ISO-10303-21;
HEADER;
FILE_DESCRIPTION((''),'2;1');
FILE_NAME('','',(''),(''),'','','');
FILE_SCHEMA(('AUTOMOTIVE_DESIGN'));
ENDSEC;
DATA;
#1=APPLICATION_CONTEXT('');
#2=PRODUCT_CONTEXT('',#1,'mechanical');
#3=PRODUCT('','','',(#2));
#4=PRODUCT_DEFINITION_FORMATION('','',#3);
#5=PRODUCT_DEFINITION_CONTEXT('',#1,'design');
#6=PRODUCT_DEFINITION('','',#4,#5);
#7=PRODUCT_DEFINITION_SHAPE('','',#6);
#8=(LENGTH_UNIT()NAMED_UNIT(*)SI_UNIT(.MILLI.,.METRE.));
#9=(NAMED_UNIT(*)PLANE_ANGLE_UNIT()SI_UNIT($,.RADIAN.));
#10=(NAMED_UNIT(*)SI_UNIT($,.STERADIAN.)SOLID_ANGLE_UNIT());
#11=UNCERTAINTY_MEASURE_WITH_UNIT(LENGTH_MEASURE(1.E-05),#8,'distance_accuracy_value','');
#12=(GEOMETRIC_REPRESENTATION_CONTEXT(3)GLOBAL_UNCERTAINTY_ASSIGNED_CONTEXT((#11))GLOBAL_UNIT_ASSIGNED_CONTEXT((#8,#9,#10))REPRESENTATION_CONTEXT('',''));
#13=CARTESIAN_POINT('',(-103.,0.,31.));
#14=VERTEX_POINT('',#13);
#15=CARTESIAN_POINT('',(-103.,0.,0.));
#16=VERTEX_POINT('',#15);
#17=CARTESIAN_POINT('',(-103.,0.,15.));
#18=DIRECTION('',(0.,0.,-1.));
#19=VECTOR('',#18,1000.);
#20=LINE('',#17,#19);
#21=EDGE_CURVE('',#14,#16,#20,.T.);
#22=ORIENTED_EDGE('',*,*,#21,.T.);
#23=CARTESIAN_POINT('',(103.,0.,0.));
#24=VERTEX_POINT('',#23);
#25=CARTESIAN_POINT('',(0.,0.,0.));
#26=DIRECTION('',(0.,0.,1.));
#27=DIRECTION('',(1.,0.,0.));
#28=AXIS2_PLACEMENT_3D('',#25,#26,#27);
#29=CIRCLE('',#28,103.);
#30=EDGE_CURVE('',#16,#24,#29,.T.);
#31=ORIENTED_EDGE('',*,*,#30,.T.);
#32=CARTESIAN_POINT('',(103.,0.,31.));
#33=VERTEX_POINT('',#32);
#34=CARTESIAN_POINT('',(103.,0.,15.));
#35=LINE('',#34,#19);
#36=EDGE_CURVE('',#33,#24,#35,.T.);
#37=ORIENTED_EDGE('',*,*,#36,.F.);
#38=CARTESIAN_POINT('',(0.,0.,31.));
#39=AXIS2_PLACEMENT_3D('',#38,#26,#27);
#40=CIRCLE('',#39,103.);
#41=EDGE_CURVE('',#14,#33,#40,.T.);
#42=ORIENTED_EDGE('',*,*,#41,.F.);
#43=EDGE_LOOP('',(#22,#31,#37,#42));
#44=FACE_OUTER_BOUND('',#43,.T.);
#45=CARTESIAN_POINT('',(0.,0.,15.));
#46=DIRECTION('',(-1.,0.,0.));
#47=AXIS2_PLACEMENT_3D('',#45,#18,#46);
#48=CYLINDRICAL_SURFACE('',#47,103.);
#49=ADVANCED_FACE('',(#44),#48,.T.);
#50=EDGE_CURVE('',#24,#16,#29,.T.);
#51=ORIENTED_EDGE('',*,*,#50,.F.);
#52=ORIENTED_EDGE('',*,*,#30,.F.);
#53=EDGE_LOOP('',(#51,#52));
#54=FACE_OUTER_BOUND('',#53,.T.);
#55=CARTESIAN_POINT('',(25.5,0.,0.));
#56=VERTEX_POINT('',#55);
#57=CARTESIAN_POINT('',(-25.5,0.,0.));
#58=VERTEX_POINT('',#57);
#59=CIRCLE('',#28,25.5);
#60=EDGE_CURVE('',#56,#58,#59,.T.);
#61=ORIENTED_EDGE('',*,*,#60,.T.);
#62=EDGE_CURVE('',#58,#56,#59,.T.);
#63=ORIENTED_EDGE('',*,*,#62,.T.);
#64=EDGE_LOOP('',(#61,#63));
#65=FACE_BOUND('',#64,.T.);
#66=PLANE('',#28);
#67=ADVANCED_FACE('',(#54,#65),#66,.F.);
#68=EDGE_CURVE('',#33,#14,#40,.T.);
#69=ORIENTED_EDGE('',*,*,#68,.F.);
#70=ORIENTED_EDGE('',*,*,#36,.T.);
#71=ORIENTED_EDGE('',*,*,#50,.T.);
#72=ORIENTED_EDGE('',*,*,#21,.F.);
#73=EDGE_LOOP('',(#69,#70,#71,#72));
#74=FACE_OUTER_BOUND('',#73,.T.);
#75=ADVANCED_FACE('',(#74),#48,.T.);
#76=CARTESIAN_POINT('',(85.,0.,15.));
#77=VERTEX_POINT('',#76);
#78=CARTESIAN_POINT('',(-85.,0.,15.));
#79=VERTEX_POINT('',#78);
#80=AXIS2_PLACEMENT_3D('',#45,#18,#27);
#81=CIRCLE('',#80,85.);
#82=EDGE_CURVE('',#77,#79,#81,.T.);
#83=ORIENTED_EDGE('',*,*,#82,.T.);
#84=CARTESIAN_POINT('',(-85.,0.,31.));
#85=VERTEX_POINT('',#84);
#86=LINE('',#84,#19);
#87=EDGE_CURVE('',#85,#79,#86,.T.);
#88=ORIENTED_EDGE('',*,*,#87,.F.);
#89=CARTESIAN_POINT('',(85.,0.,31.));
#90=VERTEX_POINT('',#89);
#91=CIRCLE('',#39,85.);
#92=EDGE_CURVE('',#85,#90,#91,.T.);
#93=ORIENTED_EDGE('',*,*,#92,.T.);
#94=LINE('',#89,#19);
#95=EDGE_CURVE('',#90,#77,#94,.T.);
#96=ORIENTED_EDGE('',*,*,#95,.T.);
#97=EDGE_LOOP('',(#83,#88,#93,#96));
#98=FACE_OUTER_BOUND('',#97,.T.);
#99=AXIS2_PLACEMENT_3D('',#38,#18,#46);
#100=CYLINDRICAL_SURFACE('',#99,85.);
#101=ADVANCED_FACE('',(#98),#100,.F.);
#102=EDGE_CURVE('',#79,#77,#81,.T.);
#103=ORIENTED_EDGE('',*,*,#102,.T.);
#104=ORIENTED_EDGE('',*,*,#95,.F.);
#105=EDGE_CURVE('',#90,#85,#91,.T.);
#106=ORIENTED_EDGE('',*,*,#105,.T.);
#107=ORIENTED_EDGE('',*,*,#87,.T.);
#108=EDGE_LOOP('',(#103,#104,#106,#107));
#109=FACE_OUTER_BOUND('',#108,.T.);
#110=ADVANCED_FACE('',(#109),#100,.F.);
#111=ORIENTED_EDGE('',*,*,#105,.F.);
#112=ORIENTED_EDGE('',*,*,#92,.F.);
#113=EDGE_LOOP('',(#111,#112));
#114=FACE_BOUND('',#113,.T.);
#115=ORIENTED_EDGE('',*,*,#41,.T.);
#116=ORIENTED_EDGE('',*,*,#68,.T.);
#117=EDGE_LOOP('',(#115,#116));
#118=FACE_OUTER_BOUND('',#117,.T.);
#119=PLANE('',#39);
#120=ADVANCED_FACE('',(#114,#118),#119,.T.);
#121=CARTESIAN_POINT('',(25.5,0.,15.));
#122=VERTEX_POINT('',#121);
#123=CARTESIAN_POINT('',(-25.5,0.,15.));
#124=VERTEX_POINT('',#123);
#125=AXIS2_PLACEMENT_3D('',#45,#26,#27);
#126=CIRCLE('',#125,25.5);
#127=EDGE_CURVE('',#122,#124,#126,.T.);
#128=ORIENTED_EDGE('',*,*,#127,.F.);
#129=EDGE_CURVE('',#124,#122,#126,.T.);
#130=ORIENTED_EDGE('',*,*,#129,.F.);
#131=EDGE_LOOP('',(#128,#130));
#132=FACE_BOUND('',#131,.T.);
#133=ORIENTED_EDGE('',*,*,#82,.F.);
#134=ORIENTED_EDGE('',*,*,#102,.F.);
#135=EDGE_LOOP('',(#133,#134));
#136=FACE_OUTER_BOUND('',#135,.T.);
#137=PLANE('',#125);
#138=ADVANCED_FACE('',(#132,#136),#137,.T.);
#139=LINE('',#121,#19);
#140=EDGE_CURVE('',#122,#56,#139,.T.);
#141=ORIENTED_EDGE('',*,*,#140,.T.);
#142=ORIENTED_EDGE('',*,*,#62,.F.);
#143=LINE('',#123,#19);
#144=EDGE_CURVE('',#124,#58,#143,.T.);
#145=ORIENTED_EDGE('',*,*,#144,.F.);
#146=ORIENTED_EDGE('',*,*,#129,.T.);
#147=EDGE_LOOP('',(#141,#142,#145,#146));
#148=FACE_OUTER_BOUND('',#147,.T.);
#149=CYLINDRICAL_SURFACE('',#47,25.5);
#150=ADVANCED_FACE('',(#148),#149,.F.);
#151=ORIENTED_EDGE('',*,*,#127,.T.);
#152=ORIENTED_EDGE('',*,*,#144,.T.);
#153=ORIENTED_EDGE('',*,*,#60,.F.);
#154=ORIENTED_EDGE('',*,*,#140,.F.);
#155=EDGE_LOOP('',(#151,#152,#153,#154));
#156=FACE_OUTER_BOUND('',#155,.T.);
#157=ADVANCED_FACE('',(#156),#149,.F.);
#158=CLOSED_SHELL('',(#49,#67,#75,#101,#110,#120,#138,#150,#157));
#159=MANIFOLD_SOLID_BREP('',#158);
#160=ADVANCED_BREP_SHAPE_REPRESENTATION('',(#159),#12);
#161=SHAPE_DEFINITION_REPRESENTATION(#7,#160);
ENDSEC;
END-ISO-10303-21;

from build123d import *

# Parameters (mm, degrees)
SKETCH1_R           = 103
SKETCH1_R_2         = 25.5
BOSS_EXTRUDE1_DEPTH = 15
SKETCH2_R           = 103
SKETCH2_R_2         = 85
BOSS_EXTRUDE2_DEPTH = 16


with BuildPart() as part:
    # Sketch1 → Boss-Extrude1 (new body)
    with BuildSketch(Plane.XY):
        Circle(SKETCH1_R)
        Circle(SKETCH1_R_2, mode=Mode.SUBTRACT)
    extrude(amount=BOSS_EXTRUDE1_DEPTH)

    # Sketch2 → Boss-Extrude2 (add)
    with BuildSketch(Plane.XY.offset(15)):
        Circle(SKETCH2_R)
        Circle(SKETCH2_R_2, mode=Mode.SUBTRACT)
    extrude(amount=BOSS_EXTRUDE2_DEPTH)


solid = part.part
